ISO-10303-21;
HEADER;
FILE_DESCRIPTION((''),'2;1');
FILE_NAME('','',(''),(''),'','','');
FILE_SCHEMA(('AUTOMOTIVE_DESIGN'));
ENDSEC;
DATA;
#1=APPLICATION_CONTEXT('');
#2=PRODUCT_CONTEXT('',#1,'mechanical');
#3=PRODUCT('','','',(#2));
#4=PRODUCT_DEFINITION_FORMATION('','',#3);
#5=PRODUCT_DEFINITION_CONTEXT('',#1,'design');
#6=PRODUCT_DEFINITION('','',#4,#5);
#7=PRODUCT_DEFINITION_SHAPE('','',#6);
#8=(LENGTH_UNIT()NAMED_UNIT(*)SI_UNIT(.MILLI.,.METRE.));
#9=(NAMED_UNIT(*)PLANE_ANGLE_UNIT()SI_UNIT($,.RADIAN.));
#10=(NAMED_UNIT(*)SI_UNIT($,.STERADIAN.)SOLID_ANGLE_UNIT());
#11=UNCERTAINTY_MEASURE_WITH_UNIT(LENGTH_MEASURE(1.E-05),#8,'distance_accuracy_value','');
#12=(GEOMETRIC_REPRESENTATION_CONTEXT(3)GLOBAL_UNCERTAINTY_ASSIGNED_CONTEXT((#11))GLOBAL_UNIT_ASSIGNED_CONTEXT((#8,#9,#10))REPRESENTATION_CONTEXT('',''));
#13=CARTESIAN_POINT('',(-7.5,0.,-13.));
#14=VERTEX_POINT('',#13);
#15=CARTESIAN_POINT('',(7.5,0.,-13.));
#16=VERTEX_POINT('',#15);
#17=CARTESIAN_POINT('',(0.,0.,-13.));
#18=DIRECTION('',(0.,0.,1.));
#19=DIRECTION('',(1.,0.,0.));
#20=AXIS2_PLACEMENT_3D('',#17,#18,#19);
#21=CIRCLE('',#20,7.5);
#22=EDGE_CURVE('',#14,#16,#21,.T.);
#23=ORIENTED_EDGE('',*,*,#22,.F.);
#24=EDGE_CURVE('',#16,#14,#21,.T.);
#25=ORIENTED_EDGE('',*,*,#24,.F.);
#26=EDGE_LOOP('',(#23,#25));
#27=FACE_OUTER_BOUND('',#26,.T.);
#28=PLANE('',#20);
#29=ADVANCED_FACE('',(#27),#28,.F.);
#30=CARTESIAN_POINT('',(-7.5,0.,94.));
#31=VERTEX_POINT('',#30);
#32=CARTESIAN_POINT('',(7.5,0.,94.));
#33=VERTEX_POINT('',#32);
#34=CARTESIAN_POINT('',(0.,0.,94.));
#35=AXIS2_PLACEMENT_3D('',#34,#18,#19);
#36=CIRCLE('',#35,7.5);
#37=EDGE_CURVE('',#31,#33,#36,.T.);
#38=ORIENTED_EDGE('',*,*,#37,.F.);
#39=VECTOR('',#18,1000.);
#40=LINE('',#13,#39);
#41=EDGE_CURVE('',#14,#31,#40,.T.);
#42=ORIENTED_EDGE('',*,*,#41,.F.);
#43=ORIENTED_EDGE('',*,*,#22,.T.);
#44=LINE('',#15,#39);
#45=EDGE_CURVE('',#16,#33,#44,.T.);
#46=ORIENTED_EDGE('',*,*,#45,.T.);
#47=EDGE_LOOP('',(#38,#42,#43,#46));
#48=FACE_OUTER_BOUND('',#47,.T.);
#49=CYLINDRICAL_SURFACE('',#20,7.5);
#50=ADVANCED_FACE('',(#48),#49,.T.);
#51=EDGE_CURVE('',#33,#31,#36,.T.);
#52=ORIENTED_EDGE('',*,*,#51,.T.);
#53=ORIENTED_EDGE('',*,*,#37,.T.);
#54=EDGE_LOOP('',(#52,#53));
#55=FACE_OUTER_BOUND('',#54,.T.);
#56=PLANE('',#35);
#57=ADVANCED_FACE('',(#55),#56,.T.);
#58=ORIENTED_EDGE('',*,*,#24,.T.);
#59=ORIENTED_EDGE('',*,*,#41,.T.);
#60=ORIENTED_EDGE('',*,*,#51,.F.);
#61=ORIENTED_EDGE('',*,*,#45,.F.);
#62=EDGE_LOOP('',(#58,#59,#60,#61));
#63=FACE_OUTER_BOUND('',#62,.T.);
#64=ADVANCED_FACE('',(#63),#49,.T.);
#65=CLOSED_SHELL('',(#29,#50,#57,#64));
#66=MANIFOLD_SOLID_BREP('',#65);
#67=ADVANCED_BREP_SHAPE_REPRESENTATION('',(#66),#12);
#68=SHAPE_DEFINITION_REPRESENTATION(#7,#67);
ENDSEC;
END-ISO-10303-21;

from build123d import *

# Parameters (mm, degrees)
BOSS_EXTRUDE1_DEPTH      = 94
BOSS_EXTRUDE1_DEPTH_BACK = 13
SKETCH1_R                = 7.5


with BuildPart() as part:
    # Sketch1 → Boss-Extrude1 (new, two sides: drawn at the far end of the back side and taken through both)
    with BuildSketch(Plane.XY.offset(-BOSS_EXTRUDE1_DEPTH_BACK)):
        Circle(SKETCH1_R)
    extrude(amount=BOSS_EXTRUDE1_DEPTH + BOSS_EXTRUDE1_DEPTH_BACK)


solid = part.part
